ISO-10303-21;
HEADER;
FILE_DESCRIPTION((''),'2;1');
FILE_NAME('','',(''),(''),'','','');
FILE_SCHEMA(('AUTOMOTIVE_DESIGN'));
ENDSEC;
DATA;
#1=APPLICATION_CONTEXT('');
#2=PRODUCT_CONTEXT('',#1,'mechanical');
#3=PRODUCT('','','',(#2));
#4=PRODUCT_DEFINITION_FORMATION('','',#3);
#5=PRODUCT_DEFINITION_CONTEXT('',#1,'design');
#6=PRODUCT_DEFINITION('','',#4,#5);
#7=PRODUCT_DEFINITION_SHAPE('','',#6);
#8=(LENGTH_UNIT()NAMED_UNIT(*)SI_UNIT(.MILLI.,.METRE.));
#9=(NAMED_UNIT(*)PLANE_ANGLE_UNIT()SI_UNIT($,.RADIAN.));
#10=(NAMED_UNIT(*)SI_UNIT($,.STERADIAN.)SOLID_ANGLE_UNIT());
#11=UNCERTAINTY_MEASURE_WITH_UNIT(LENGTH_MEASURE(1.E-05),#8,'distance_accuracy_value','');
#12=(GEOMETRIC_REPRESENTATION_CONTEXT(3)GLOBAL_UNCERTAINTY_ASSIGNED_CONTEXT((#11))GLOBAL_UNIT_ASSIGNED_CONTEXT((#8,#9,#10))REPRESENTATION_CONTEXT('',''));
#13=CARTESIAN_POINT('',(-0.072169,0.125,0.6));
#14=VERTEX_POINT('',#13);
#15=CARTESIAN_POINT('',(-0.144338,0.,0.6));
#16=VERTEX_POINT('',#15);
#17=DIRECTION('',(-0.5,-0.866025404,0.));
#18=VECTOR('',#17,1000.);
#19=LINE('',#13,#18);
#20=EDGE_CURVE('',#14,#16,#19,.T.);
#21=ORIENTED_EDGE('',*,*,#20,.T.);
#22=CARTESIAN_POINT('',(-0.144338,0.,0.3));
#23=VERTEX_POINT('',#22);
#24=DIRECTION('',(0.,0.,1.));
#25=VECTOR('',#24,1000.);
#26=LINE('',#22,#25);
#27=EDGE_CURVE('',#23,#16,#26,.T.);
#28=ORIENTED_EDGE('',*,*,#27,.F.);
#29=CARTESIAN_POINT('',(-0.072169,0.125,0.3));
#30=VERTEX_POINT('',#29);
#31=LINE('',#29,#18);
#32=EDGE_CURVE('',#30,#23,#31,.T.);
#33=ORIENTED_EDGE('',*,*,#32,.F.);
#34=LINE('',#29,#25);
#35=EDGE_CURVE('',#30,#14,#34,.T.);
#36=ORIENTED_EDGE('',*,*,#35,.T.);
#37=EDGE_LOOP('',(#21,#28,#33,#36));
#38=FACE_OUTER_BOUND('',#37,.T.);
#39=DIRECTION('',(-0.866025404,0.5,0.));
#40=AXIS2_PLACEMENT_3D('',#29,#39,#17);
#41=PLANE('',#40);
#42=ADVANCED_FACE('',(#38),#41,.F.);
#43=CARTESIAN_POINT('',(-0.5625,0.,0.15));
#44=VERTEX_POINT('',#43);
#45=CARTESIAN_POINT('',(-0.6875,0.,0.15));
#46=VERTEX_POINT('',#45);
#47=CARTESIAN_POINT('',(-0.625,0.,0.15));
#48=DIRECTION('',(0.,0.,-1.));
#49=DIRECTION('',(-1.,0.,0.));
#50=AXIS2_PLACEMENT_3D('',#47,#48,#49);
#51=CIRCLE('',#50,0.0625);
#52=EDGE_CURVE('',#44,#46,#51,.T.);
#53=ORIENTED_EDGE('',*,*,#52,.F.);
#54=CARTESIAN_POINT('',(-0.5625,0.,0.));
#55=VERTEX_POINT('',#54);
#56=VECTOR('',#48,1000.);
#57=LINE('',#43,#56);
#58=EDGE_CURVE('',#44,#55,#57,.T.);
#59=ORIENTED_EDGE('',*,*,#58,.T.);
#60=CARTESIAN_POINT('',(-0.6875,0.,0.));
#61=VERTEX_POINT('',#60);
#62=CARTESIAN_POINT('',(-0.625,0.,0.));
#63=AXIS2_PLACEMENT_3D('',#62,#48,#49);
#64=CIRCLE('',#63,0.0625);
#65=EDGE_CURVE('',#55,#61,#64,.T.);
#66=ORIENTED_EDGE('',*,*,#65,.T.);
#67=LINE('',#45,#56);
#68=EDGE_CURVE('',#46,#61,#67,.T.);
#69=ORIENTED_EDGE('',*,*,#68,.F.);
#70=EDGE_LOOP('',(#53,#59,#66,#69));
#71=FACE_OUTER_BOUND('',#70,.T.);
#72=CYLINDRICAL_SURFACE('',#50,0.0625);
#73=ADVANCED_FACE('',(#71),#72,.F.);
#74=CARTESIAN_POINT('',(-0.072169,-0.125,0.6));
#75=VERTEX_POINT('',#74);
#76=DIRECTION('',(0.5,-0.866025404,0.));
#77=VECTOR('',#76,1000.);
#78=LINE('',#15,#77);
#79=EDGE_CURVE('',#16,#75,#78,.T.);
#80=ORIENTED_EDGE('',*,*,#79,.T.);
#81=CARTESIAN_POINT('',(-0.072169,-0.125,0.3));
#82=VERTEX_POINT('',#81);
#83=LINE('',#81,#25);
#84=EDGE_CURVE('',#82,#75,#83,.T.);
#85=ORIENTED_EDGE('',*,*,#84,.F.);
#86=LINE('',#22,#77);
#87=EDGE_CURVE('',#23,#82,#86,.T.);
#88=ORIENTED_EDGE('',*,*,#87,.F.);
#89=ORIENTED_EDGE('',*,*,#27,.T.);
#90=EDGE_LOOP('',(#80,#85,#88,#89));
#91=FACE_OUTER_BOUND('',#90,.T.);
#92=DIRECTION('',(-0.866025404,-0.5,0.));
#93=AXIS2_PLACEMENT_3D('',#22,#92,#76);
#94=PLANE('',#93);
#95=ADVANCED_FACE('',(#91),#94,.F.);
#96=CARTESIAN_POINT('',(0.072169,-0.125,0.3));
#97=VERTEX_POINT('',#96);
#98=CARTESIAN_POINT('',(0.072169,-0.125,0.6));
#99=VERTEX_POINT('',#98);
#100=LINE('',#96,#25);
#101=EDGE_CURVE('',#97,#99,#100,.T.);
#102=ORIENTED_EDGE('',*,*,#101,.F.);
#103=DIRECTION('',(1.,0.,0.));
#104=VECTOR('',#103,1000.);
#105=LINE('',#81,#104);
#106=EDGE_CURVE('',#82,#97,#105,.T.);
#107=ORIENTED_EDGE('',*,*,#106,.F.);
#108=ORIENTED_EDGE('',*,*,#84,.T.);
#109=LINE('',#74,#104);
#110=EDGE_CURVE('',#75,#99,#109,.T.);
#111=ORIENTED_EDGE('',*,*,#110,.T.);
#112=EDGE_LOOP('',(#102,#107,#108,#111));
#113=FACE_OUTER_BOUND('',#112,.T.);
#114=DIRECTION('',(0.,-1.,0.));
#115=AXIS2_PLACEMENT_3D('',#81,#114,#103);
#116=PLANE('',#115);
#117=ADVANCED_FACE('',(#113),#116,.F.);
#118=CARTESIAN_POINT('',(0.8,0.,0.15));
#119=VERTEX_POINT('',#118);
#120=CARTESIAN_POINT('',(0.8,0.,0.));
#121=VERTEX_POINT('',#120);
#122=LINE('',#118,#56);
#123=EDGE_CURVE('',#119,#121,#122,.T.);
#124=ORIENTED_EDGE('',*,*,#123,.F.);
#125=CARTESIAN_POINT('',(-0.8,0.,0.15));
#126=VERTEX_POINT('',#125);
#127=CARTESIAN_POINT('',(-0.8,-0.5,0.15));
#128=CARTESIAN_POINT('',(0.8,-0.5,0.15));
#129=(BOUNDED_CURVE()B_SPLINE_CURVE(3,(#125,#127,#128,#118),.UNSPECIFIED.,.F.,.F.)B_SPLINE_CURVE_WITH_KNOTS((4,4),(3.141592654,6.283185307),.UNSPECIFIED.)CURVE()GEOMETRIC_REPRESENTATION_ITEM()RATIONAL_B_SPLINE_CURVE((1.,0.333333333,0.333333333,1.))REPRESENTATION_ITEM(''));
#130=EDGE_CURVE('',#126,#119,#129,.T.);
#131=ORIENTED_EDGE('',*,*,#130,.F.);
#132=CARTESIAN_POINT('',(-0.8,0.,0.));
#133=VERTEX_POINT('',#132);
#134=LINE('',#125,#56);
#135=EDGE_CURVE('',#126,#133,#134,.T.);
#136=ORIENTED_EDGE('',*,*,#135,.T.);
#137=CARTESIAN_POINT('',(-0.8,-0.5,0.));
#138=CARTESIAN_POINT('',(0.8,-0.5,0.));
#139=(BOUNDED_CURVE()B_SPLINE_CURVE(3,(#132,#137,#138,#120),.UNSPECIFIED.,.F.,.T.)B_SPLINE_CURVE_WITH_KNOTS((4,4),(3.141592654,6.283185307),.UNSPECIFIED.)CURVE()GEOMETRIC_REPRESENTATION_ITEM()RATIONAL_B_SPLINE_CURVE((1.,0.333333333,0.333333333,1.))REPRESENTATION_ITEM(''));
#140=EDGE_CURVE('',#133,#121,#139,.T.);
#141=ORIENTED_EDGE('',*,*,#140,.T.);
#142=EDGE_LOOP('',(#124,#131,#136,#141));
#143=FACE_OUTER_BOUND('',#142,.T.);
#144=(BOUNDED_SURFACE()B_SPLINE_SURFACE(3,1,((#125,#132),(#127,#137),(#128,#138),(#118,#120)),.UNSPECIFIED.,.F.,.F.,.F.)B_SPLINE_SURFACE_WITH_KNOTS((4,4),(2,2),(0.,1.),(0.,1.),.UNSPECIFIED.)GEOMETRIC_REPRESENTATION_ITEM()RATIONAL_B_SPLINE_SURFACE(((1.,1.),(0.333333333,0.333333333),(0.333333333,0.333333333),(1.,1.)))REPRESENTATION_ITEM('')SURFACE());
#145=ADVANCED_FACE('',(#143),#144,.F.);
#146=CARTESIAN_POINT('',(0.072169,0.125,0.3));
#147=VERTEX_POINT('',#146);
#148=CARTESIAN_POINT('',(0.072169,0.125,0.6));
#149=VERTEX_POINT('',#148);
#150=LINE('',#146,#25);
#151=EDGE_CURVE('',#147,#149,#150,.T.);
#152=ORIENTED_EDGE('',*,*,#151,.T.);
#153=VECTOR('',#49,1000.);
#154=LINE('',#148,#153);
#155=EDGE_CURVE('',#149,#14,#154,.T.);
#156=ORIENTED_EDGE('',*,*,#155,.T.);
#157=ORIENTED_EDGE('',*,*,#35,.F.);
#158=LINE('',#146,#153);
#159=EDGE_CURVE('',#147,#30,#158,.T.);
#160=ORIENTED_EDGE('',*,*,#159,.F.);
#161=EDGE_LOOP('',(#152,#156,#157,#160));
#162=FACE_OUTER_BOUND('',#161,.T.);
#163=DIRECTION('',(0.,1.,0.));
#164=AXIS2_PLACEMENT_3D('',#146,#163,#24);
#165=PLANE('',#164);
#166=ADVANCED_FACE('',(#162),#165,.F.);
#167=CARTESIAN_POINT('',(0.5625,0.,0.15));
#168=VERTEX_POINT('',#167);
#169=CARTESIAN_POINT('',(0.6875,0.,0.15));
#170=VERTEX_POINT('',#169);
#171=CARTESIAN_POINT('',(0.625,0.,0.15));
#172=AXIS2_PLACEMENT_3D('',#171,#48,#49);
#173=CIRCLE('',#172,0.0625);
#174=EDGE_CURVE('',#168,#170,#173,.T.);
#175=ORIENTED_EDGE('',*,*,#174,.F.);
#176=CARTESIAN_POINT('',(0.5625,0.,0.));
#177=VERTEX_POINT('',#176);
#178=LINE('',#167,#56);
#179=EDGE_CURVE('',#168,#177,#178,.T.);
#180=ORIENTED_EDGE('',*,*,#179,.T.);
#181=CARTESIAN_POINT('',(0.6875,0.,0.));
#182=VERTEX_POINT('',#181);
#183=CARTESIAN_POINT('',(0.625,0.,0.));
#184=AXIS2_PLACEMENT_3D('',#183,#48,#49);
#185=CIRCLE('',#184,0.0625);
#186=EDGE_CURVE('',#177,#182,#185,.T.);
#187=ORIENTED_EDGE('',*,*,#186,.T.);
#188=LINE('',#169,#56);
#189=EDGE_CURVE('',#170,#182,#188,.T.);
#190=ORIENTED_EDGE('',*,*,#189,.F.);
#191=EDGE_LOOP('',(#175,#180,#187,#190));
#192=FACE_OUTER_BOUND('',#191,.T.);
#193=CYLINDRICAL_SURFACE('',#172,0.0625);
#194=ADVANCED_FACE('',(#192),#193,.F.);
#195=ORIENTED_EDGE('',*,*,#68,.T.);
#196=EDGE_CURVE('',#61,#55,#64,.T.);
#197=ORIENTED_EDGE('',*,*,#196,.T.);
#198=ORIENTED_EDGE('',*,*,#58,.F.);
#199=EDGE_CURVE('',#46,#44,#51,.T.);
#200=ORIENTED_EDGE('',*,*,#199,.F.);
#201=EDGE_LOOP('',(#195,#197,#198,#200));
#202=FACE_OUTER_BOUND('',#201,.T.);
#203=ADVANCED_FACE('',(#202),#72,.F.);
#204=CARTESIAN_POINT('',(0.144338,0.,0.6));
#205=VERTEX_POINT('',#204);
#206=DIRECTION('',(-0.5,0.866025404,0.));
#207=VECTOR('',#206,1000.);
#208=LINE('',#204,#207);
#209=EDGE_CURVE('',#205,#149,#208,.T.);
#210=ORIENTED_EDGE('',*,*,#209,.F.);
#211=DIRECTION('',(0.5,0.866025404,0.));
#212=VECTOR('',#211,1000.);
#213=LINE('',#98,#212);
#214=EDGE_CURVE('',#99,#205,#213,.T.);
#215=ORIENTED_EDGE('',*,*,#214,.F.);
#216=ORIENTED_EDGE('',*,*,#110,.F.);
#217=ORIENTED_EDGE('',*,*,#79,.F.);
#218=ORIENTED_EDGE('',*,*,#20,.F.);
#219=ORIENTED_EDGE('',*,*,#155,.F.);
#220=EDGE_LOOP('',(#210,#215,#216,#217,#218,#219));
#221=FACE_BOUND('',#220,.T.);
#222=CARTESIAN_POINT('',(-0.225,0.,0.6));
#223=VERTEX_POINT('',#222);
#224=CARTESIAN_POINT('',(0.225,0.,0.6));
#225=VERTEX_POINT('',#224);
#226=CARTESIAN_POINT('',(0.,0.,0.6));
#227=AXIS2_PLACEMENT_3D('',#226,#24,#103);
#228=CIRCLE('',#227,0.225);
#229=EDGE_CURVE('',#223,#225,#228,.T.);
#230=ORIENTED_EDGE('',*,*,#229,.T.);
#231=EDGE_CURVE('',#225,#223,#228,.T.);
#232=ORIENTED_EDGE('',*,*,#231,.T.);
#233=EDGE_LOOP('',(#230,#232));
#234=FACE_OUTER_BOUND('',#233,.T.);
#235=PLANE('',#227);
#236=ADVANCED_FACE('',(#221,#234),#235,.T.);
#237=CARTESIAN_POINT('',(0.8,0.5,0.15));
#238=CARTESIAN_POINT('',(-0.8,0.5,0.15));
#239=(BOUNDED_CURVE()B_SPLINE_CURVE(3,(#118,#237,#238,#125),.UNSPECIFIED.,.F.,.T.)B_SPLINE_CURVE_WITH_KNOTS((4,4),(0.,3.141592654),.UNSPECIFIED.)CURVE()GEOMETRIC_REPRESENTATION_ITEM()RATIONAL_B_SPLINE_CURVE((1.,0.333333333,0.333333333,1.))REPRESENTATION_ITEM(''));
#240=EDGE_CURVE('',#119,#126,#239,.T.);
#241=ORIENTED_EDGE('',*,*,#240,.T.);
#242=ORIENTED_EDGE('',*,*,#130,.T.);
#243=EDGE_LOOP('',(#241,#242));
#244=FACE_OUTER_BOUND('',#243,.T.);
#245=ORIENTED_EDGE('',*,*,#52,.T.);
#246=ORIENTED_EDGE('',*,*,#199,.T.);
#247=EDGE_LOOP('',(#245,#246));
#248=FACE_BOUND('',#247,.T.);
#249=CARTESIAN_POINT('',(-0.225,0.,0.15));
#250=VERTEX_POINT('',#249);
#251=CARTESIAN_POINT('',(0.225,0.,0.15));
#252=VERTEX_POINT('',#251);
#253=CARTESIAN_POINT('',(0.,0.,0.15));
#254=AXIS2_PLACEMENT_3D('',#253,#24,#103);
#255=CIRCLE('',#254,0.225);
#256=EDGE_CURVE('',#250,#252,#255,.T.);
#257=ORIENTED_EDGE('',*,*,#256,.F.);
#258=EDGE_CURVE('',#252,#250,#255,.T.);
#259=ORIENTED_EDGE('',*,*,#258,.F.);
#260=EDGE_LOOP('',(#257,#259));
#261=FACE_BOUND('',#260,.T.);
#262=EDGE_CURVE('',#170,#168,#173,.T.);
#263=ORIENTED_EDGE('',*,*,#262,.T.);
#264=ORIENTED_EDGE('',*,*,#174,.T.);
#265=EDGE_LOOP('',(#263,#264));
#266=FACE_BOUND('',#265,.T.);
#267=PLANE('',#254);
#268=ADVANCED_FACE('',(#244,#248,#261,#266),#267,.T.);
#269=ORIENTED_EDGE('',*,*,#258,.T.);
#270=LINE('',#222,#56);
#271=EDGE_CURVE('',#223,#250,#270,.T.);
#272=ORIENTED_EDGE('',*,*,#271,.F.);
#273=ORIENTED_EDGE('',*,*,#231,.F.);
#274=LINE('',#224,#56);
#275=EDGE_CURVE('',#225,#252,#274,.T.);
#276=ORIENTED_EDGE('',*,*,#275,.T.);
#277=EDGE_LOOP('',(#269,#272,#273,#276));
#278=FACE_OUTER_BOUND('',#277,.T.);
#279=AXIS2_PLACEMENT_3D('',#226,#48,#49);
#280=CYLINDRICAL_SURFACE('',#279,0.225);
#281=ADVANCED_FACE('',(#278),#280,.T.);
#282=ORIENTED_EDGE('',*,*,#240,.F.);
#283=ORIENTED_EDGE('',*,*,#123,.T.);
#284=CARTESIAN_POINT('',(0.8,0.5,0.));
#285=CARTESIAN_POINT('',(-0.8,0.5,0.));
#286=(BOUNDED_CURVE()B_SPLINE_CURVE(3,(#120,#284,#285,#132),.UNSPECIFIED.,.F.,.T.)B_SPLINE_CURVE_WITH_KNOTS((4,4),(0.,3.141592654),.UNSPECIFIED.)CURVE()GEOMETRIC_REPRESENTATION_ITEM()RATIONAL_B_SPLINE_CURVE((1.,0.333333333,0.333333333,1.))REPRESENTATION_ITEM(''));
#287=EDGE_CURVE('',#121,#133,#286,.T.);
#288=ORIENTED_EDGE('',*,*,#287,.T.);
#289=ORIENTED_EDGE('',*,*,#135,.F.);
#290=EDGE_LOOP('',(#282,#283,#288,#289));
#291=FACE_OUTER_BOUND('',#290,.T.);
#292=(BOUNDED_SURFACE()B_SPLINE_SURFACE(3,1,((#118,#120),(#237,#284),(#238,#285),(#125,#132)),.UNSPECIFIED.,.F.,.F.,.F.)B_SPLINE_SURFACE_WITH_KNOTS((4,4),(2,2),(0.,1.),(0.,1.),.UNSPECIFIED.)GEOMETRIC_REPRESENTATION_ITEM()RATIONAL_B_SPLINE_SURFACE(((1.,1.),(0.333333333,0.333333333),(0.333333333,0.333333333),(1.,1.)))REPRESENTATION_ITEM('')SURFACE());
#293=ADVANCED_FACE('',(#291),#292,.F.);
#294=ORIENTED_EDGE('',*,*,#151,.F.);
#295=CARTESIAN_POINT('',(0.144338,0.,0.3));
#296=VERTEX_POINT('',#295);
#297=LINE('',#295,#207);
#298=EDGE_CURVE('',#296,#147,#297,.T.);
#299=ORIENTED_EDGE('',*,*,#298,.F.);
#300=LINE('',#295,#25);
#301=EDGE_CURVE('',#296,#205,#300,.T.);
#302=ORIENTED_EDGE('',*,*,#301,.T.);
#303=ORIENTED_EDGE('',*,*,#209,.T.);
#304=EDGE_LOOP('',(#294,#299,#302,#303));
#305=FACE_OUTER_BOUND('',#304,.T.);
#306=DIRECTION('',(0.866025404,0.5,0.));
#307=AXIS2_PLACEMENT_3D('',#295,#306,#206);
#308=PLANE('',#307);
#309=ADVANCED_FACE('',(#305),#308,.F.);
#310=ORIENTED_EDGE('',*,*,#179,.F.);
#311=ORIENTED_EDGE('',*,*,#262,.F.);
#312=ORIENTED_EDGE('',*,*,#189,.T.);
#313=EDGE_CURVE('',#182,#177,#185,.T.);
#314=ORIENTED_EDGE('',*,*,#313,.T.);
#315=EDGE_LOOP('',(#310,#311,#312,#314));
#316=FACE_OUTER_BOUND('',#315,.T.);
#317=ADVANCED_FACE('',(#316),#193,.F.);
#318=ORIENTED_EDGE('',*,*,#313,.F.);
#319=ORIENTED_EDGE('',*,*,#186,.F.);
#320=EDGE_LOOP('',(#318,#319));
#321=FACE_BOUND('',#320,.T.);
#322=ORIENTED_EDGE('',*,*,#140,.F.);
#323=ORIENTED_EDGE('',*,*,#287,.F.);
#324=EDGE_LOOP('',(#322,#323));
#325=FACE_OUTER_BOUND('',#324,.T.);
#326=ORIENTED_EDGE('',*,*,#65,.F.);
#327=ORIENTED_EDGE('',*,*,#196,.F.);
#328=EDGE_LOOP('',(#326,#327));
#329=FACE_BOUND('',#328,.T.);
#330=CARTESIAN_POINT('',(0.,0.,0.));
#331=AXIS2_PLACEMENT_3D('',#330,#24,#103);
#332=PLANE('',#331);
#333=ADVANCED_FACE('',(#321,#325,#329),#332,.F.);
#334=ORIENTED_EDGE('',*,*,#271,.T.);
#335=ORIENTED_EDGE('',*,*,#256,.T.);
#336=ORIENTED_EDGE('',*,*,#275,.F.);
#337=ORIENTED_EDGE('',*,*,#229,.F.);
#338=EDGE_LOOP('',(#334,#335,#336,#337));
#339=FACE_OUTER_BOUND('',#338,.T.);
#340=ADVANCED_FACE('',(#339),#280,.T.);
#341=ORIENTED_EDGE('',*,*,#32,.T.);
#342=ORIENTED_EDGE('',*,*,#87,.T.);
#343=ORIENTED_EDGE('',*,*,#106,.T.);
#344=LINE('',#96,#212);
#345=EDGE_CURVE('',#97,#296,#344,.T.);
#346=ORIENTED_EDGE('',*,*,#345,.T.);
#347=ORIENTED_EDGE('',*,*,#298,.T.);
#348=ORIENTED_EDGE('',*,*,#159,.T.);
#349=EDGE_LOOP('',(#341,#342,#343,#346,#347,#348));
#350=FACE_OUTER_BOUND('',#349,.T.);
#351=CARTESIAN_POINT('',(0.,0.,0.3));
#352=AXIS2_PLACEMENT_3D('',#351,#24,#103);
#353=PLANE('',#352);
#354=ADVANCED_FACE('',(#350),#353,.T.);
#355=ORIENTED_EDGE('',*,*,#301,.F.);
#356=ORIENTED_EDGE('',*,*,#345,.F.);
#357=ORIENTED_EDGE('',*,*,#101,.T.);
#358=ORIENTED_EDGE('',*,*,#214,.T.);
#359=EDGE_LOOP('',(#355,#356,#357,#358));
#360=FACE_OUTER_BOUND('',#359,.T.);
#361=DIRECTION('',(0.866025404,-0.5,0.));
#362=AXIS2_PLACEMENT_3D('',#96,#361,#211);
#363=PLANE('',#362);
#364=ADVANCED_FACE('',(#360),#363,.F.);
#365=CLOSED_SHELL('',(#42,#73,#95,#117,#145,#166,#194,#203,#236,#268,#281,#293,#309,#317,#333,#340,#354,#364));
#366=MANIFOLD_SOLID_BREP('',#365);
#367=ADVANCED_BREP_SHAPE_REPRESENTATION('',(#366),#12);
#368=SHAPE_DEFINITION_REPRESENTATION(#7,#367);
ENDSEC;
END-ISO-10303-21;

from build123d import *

# Parameters (mm, degrees)
FLANGE_OUTLINE_SKETCH_RX    = 0.8
FLANGE_OUTLINE_SKETCH_RY    = 0.25
OVAL_FLANGE_DEPTH           = 0.15
HUB_AND_HEX_SOCKET_SKETCH_R = 0.225
CYLINDRICAL_HUB_DEPTH       = 0.45
HEX_START                   = 0.45
HEX_SOCKET_DEPTH            = 0.3
MOUNTING_HOLES_SKETCH_R     = 0.0625
MOUNTING_HOLES_2X_DEPTH     = 0.15


with BuildPart() as part:
    # Flange Outline Sketch → Oval Flange (new body)
    with BuildSketch(Plane.XY):
        with Locations((0, 0)):
            Ellipse(FLANGE_OUTLINE_SKETCH_RX, FLANGE_OUTLINE_SKETCH_RY)
    extrude(amount=OVAL_FLANGE_DEPTH)

    # Hub and Hex Socket Sketch → Cylindrical Hub (add)
    with BuildSketch(Plane.XY.offset(0.15)):
        Circle(HUB_AND_HEX_SOCKET_SKETCH_R)
    extrude(amount=CYLINDRICAL_HUB_DEPTH)

    # Sketch2_4 → Hex Socket (cut)
    with BuildSketch(Plane.XY.offset(0.15).offset(HEX_START)):
        Polygon((0.144337567, 0), (0.072168784, 0.125), (-0.072168784, 0.125), (-0.144337567, 0), (-0.072168784, -0.125), (0.072168784, -0.125), align=None)
    extrude(amount=-HEX_SOCKET_DEPTH, mode=Mode.SUBTRACT)

    # Mounting Holes Sketch → Mounting Holes 2x (cut)
    with BuildSketch(Plane(origin=(0, 0, 0), x_dir=(-1, 0, 0), z_dir=(0, 0, -1))):
        with Locations((-0.625, 0)):
            Circle(MOUNTING_HOLES_SKETCH_R)
        with Locations((0.625, 0)):
            Circle(MOUNTING_HOLES_SKETCH_R)
    extrude(amount=-MOUNTING_HOLES_2X_DEPTH, mode=Mode.SUBTRACT)


solid = part.part
